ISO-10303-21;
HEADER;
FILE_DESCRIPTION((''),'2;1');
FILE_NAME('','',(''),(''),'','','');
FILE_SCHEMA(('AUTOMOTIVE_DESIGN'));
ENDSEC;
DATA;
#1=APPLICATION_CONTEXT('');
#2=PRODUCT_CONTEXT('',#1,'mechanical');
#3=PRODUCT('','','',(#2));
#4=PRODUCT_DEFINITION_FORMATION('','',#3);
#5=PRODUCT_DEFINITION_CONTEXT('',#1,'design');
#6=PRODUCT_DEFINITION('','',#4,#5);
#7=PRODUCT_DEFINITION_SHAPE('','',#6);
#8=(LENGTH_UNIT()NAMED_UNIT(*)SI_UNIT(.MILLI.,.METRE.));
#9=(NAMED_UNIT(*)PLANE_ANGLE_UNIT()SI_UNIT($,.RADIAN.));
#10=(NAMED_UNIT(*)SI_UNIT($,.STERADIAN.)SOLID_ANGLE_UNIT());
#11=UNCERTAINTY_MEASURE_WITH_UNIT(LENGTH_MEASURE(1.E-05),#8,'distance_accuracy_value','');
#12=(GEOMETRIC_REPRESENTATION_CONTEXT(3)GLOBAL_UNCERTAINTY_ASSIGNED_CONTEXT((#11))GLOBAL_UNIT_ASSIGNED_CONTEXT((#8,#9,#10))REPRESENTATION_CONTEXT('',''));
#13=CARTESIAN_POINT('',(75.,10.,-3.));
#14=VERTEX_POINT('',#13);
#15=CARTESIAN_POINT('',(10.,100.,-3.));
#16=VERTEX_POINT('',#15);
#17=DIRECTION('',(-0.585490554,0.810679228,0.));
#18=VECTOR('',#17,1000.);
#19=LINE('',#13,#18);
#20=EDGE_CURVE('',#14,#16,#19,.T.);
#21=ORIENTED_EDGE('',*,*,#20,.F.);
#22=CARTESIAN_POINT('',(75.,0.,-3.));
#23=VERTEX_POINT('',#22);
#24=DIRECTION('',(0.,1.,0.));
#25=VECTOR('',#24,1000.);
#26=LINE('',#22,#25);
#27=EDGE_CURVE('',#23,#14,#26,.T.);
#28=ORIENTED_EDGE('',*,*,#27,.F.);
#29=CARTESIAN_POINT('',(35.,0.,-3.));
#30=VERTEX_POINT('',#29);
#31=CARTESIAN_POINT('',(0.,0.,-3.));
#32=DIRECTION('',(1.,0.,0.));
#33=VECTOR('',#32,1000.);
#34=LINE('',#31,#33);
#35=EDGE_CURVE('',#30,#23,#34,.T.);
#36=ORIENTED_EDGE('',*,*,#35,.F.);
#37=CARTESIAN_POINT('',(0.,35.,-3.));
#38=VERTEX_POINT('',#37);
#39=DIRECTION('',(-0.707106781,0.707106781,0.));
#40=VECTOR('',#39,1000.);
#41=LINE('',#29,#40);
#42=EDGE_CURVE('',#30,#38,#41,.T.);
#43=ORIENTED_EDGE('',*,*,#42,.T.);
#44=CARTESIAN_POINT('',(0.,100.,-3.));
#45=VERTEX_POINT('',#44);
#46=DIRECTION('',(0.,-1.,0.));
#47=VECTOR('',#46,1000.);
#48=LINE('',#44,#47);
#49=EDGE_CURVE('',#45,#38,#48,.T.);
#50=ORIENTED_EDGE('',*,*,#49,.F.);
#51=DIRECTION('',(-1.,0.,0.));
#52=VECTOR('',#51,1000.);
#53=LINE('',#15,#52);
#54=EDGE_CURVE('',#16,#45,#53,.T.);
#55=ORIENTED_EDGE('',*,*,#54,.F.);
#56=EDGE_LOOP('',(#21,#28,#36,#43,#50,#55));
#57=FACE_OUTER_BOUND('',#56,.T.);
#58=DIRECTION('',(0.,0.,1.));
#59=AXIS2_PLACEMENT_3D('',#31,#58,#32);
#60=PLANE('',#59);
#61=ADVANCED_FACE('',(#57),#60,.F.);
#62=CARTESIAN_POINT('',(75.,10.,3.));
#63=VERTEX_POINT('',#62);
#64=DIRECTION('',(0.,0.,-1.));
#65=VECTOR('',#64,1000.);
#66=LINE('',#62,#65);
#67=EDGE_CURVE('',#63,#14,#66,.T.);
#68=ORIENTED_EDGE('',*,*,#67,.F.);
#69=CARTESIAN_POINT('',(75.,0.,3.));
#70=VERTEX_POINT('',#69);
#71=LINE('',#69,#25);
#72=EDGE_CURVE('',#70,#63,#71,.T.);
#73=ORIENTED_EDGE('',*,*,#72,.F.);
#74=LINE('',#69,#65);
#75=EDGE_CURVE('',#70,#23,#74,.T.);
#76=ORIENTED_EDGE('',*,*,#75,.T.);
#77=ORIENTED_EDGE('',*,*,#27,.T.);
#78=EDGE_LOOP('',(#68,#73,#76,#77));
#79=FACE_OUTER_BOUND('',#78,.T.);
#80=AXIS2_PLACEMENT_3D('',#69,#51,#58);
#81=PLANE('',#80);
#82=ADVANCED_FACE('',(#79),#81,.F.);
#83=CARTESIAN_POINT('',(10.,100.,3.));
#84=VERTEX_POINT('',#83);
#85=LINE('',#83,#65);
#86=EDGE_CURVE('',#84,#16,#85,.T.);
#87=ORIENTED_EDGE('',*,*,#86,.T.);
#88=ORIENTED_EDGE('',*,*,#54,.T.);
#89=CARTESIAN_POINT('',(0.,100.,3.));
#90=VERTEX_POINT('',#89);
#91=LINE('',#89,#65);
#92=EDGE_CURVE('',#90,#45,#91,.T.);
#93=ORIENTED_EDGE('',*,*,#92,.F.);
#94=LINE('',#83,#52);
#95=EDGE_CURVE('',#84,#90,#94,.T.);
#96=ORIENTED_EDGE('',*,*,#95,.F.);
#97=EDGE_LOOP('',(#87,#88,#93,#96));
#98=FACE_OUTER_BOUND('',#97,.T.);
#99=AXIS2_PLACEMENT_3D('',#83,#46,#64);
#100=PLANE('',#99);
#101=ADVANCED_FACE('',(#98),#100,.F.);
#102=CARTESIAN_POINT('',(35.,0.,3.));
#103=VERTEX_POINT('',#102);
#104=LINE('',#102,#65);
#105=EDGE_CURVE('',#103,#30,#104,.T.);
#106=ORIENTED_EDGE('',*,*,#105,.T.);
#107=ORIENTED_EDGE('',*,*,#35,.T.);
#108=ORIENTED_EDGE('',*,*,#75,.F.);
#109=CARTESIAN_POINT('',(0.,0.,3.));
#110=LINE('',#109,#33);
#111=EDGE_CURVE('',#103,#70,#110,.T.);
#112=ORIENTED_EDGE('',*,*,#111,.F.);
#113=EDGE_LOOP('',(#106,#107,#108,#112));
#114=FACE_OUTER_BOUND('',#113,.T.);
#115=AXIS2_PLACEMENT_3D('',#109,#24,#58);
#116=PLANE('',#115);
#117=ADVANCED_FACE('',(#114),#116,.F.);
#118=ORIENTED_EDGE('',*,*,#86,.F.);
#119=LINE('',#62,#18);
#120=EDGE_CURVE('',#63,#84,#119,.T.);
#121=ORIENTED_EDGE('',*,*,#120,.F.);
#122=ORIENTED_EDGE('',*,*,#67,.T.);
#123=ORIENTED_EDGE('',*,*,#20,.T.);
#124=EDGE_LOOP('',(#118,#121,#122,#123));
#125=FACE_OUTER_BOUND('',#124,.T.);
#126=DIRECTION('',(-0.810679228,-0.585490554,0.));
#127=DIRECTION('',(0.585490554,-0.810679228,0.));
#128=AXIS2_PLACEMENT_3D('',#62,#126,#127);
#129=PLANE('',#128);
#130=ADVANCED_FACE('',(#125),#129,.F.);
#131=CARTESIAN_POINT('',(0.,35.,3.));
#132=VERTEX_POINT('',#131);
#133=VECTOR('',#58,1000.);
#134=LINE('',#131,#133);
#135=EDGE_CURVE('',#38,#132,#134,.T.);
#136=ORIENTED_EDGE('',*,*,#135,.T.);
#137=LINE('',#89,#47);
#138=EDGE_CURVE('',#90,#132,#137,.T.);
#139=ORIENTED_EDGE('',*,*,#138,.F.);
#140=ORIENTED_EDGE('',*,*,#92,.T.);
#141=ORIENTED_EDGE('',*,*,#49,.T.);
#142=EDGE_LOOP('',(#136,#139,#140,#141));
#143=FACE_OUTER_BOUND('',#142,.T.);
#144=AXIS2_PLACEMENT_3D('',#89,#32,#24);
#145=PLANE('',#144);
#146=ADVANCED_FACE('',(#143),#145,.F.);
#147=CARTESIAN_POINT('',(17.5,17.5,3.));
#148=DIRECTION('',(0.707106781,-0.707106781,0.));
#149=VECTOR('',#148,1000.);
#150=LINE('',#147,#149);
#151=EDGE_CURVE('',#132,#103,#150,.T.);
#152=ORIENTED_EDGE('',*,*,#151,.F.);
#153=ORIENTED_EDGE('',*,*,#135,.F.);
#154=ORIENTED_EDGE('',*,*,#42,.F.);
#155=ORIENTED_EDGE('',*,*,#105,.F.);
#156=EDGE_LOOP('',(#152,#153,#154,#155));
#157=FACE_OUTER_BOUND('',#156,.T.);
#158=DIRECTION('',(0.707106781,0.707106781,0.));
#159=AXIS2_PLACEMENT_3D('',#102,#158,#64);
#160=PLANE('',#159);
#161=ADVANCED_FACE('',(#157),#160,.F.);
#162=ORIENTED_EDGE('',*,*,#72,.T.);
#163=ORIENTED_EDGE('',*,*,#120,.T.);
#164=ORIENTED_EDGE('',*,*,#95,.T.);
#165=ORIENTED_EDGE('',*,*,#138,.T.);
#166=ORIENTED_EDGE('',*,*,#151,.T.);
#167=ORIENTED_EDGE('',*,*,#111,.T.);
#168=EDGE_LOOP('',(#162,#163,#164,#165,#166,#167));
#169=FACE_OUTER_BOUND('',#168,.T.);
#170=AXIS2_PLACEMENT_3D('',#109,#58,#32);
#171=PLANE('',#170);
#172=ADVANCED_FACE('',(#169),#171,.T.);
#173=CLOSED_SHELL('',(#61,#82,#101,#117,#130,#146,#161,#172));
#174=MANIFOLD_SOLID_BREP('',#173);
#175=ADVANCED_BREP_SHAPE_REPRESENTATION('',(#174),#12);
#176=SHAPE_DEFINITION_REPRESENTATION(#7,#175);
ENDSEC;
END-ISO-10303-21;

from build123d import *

# Parameters (mm, degrees)
BOSS_EXTRUDE1_DEPTH = 3
CHAMFER1_SIZE       = 35


with BuildPart() as part:
    # Sketch1 → Boss-Extrude1 (new, symmetric)
    with BuildSketch(Plane.XY):
        Polygon((0, 100), (0, 0), (75, 0), (75, 10), (10, 100), align=None)
    extrude(amount=BOSS_EXTRUDE1_DEPTH, both=True)

    # Chamfer1
    chamfer1_edges = [part.edges().sort_by_distance(p)[0] for p in [
        (0, 0, 0),
    ]]
    chamfer(chamfer1_edges, length=CHAMFER1_SIZE)


solid = part.part
